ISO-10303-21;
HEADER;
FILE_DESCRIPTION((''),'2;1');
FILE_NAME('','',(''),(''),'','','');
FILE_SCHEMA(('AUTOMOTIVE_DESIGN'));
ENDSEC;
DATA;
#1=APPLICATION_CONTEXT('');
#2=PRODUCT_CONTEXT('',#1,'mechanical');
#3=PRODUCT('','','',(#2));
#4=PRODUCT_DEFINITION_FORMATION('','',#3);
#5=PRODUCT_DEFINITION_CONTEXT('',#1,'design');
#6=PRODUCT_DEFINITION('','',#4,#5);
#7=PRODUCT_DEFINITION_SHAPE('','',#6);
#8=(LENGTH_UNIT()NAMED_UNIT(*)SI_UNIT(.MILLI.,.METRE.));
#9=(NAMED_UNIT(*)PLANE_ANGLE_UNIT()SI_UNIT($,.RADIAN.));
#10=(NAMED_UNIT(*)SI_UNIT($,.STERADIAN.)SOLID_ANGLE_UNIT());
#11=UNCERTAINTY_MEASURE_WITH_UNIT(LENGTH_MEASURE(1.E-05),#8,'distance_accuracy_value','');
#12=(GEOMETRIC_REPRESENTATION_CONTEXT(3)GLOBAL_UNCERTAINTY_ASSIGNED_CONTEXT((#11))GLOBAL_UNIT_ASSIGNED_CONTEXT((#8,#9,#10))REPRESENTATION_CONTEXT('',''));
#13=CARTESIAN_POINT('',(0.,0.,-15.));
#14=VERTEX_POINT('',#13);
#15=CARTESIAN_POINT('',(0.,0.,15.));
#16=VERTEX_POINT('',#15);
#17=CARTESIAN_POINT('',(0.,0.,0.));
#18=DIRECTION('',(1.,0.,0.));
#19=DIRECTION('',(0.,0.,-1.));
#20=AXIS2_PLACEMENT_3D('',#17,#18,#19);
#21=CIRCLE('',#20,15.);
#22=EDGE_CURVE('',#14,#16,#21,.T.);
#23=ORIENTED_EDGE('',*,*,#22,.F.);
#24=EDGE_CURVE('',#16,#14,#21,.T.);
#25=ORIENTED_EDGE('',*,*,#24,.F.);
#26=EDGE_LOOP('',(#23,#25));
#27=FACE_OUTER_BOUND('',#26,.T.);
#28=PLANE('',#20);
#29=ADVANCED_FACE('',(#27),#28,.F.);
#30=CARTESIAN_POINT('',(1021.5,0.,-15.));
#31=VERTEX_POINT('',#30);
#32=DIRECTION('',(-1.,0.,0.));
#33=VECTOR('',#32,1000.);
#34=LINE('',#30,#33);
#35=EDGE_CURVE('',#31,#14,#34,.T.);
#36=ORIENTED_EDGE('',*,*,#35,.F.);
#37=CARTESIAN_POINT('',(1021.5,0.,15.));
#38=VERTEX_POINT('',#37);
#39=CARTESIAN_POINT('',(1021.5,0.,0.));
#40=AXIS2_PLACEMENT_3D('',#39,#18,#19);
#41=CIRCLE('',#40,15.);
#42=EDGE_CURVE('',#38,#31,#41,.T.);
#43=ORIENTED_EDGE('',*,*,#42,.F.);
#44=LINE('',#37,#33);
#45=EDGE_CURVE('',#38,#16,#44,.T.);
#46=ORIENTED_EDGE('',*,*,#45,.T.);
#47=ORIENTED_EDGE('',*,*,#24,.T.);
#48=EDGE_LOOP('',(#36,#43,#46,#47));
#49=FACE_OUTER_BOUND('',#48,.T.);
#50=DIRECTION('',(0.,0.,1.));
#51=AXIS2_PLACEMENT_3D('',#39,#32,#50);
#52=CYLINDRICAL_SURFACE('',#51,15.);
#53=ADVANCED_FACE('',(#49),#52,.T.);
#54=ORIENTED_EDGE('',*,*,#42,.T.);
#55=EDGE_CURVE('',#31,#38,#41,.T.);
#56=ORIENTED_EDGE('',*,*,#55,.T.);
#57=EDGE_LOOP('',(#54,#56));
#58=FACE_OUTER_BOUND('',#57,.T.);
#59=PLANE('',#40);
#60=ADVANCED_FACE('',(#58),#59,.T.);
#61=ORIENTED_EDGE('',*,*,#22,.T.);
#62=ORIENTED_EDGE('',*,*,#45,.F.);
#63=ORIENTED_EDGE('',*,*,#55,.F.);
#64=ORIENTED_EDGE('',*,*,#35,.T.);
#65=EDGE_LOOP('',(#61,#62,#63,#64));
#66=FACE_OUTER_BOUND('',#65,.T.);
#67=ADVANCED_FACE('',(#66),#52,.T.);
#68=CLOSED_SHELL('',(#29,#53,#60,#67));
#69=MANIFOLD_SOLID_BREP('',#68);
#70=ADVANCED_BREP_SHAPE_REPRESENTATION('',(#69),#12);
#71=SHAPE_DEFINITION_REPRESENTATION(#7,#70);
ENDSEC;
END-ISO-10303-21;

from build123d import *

# Parameters (mm, degrees)
SKETCH12_R          = 15
SKETCH12_R_2        = 12
MEMBER_30X3_1_DEPTH = 1021.5
SKETCH_5_R          = 12
EXTRUDE_2_DEPTH     = 1021.5


with BuildPart() as part:
    # Sketch12 → Member 30X3_1 (new body)
    with BuildSketch(Plane.YZ):
        Circle(SKETCH12_R)
        Circle(SKETCH12_R_2, mode=Mode.SUBTRACT)
    extrude(amount=MEMBER_30X3_1_DEPTH)

    # 草图5 → 凸台-拉伸2 (add, through all)
    with BuildSketch(Plane(origin=(1021.5, 0, 0), x_dir=(0, 0, -1), z_dir=(1, 0, 0))):
        Circle(SKETCH_5_R)
    extrude(amount=-EXTRUDE_2_DEPTH)


solid = part.part
